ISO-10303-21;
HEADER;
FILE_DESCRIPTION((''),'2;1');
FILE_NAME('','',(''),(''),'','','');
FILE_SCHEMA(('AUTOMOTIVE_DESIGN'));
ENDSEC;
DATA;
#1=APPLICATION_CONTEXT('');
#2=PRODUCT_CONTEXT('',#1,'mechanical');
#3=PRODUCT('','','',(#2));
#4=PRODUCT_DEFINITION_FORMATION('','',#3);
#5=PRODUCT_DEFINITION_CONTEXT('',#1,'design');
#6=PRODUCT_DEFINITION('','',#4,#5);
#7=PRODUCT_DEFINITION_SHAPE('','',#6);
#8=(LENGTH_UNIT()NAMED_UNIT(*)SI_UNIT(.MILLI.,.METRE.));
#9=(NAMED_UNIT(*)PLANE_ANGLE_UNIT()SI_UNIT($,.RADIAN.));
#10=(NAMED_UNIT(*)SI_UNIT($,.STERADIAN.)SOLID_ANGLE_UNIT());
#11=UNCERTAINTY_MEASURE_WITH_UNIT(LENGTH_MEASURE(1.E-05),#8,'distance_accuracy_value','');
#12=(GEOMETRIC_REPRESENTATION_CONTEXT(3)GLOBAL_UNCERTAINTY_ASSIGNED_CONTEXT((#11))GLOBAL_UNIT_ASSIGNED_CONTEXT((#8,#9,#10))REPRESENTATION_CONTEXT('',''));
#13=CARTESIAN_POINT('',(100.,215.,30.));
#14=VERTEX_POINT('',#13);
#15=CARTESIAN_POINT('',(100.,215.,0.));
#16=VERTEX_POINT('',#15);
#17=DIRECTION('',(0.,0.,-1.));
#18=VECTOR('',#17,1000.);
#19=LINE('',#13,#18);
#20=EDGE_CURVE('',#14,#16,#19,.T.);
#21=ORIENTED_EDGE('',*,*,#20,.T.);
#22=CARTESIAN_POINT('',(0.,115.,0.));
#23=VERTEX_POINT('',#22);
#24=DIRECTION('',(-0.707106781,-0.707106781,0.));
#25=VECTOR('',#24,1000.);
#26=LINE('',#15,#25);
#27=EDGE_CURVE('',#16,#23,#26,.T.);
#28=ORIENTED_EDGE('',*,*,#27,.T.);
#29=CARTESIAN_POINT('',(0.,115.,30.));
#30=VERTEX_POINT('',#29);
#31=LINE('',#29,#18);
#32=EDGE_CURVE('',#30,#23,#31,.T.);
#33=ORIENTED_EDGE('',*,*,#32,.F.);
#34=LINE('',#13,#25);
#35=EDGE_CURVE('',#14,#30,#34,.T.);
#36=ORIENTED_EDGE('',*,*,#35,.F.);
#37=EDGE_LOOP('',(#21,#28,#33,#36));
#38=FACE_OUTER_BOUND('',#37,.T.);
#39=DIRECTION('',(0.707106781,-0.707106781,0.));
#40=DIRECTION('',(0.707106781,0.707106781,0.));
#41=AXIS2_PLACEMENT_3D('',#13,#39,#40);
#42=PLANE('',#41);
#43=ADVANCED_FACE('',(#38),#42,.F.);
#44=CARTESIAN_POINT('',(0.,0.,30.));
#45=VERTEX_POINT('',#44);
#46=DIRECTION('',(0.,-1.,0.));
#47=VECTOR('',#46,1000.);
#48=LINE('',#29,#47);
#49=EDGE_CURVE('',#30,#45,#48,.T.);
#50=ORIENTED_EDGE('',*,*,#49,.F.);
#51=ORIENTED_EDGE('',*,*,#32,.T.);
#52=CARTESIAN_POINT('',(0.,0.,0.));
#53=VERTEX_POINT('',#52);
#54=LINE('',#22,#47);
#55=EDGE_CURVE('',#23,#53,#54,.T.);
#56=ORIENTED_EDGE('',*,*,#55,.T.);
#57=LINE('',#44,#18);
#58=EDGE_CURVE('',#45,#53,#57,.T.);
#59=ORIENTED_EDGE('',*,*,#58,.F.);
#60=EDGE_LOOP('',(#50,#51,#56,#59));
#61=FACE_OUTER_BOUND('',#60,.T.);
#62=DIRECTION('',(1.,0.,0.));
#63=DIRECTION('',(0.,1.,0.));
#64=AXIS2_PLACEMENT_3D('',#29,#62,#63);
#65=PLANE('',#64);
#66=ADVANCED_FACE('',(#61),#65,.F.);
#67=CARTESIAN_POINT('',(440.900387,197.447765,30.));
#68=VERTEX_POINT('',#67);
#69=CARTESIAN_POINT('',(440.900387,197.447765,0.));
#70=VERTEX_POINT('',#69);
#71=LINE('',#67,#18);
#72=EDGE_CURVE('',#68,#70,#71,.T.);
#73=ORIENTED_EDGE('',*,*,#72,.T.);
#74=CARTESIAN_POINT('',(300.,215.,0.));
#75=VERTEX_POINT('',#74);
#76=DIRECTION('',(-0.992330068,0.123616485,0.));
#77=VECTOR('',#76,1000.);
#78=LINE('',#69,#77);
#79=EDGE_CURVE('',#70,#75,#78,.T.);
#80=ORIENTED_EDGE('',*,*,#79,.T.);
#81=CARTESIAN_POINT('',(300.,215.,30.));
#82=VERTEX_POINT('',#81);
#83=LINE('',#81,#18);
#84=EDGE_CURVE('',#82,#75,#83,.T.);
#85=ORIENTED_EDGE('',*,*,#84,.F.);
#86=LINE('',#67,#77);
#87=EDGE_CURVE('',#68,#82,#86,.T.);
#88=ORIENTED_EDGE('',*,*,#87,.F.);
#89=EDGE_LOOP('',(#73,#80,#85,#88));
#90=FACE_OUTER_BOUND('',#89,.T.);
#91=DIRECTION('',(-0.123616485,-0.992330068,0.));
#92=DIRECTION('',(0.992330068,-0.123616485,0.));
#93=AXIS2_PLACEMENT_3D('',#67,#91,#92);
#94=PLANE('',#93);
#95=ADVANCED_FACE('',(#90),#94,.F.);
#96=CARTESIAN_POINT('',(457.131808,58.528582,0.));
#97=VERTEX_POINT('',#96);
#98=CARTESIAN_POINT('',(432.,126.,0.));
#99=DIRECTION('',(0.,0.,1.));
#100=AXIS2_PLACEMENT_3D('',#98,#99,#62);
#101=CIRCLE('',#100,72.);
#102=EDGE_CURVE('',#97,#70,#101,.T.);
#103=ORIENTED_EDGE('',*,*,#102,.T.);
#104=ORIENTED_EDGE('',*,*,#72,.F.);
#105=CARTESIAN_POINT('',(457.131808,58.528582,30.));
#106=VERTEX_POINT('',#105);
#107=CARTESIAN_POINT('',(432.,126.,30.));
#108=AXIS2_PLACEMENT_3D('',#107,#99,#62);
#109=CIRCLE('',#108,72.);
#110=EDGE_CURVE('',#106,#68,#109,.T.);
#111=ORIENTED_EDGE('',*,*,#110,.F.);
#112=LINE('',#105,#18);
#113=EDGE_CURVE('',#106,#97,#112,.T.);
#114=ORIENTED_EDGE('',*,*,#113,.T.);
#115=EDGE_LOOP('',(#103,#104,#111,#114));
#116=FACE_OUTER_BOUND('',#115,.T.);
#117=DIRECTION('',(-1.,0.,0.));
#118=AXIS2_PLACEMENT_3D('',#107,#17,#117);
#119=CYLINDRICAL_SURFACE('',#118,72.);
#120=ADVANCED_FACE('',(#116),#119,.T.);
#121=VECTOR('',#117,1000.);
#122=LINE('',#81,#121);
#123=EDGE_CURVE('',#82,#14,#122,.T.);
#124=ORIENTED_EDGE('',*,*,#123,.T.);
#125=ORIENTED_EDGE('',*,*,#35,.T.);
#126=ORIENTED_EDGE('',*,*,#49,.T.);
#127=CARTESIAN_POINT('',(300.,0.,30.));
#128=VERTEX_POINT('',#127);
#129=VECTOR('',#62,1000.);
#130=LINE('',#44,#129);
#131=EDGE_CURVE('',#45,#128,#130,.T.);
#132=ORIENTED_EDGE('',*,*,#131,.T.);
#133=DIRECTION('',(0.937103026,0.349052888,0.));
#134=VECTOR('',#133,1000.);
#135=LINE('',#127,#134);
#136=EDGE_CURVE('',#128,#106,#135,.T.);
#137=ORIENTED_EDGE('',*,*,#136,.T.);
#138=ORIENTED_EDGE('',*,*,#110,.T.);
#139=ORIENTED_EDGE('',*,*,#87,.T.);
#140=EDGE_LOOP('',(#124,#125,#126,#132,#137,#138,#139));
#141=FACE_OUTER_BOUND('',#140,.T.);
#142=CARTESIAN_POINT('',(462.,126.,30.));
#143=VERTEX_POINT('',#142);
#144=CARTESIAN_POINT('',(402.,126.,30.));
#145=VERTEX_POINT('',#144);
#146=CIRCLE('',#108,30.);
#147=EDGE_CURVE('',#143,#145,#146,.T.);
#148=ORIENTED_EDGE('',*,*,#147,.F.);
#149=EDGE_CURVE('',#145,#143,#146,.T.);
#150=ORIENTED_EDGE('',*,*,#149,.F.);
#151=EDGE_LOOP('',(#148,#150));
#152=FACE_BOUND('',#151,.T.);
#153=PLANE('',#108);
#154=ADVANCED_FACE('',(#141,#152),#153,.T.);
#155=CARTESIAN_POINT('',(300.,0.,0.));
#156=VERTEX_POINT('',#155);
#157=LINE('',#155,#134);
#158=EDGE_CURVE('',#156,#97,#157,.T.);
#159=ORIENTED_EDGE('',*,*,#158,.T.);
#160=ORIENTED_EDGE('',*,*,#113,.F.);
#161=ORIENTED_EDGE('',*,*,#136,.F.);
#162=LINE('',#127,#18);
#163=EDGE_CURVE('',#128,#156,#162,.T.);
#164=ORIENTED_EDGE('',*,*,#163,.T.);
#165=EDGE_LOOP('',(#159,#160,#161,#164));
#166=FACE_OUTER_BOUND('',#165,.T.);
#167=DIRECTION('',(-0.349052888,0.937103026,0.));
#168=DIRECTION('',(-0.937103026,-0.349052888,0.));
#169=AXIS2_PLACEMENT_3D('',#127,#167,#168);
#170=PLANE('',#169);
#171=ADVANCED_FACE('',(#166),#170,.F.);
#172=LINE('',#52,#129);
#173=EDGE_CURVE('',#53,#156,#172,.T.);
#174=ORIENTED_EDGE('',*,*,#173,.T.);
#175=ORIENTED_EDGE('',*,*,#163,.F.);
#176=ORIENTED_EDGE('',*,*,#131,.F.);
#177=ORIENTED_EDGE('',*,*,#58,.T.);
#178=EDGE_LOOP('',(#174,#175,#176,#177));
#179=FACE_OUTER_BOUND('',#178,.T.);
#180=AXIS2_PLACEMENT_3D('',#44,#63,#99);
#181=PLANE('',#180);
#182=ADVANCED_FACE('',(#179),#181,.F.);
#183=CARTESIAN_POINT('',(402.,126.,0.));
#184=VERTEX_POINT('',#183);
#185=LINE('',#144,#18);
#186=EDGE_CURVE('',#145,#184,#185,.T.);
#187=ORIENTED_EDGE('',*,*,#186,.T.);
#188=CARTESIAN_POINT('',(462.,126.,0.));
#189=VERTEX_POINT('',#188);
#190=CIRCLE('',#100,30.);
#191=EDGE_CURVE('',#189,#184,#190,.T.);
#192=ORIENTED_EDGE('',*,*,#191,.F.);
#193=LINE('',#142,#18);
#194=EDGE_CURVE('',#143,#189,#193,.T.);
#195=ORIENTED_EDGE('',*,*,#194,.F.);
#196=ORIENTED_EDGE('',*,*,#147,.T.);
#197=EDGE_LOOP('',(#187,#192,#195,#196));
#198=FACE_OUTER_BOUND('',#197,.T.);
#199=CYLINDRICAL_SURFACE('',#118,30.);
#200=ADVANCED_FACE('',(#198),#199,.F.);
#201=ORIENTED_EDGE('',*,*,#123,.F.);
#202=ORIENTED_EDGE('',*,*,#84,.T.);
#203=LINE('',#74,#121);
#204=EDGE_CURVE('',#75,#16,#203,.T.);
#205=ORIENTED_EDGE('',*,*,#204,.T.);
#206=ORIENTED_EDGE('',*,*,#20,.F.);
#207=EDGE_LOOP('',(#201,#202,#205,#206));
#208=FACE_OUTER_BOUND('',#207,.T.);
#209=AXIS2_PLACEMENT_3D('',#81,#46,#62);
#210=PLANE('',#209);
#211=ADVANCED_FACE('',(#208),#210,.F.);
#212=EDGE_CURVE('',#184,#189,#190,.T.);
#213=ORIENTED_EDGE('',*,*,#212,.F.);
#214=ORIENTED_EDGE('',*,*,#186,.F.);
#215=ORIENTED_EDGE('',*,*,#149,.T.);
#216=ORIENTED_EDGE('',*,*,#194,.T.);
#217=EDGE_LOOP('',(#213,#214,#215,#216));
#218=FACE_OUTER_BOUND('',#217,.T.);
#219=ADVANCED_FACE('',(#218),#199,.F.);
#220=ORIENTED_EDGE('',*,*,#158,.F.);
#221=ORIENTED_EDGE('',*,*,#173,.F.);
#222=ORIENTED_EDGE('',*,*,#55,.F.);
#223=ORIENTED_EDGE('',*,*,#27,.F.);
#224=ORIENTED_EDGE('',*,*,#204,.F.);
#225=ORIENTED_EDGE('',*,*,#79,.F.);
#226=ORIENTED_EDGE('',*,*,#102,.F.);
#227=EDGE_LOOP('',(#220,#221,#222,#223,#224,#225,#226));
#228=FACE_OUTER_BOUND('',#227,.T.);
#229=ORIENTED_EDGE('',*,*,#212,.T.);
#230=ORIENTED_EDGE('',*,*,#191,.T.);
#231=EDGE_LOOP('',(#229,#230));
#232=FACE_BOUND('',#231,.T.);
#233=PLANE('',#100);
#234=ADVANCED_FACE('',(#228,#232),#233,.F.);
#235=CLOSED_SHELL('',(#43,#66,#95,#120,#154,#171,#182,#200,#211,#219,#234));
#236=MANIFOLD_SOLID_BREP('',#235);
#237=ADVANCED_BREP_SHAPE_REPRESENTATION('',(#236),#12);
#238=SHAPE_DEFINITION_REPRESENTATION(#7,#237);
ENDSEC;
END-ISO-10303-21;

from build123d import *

# Parameters (mm, degrees)
SKETCH1_R           = 30
BOSS_EXTRUDE1_DEPTH = 30


with BuildPart() as part:
    # Sketch1 → Boss-Extrude1 (new body)
    with BuildSketch(Plane.XY):
        with BuildLine():
            Line((0, 0), (300, 0))
            Line((300, 0), (457.131807961, 58.528582136))
            ThreePointArc((457.131807961, 58.528582136), (503.513512073, 134.355692129), (440.900386954, 197.44776492))
            Line((440.900386954, 197.44776492), (300, 215))
            Line((300, 215), (100, 215))
            Line((100, 215), (0, 115))
            Line((0, 115), (0, 0))
        make_face()
        with Locations((432, 126)):
            Circle(SKETCH1_R, mode=Mode.SUBTRACT)
    extrude(amount=BOSS_EXTRUDE1_DEPTH)


solid = part.part
